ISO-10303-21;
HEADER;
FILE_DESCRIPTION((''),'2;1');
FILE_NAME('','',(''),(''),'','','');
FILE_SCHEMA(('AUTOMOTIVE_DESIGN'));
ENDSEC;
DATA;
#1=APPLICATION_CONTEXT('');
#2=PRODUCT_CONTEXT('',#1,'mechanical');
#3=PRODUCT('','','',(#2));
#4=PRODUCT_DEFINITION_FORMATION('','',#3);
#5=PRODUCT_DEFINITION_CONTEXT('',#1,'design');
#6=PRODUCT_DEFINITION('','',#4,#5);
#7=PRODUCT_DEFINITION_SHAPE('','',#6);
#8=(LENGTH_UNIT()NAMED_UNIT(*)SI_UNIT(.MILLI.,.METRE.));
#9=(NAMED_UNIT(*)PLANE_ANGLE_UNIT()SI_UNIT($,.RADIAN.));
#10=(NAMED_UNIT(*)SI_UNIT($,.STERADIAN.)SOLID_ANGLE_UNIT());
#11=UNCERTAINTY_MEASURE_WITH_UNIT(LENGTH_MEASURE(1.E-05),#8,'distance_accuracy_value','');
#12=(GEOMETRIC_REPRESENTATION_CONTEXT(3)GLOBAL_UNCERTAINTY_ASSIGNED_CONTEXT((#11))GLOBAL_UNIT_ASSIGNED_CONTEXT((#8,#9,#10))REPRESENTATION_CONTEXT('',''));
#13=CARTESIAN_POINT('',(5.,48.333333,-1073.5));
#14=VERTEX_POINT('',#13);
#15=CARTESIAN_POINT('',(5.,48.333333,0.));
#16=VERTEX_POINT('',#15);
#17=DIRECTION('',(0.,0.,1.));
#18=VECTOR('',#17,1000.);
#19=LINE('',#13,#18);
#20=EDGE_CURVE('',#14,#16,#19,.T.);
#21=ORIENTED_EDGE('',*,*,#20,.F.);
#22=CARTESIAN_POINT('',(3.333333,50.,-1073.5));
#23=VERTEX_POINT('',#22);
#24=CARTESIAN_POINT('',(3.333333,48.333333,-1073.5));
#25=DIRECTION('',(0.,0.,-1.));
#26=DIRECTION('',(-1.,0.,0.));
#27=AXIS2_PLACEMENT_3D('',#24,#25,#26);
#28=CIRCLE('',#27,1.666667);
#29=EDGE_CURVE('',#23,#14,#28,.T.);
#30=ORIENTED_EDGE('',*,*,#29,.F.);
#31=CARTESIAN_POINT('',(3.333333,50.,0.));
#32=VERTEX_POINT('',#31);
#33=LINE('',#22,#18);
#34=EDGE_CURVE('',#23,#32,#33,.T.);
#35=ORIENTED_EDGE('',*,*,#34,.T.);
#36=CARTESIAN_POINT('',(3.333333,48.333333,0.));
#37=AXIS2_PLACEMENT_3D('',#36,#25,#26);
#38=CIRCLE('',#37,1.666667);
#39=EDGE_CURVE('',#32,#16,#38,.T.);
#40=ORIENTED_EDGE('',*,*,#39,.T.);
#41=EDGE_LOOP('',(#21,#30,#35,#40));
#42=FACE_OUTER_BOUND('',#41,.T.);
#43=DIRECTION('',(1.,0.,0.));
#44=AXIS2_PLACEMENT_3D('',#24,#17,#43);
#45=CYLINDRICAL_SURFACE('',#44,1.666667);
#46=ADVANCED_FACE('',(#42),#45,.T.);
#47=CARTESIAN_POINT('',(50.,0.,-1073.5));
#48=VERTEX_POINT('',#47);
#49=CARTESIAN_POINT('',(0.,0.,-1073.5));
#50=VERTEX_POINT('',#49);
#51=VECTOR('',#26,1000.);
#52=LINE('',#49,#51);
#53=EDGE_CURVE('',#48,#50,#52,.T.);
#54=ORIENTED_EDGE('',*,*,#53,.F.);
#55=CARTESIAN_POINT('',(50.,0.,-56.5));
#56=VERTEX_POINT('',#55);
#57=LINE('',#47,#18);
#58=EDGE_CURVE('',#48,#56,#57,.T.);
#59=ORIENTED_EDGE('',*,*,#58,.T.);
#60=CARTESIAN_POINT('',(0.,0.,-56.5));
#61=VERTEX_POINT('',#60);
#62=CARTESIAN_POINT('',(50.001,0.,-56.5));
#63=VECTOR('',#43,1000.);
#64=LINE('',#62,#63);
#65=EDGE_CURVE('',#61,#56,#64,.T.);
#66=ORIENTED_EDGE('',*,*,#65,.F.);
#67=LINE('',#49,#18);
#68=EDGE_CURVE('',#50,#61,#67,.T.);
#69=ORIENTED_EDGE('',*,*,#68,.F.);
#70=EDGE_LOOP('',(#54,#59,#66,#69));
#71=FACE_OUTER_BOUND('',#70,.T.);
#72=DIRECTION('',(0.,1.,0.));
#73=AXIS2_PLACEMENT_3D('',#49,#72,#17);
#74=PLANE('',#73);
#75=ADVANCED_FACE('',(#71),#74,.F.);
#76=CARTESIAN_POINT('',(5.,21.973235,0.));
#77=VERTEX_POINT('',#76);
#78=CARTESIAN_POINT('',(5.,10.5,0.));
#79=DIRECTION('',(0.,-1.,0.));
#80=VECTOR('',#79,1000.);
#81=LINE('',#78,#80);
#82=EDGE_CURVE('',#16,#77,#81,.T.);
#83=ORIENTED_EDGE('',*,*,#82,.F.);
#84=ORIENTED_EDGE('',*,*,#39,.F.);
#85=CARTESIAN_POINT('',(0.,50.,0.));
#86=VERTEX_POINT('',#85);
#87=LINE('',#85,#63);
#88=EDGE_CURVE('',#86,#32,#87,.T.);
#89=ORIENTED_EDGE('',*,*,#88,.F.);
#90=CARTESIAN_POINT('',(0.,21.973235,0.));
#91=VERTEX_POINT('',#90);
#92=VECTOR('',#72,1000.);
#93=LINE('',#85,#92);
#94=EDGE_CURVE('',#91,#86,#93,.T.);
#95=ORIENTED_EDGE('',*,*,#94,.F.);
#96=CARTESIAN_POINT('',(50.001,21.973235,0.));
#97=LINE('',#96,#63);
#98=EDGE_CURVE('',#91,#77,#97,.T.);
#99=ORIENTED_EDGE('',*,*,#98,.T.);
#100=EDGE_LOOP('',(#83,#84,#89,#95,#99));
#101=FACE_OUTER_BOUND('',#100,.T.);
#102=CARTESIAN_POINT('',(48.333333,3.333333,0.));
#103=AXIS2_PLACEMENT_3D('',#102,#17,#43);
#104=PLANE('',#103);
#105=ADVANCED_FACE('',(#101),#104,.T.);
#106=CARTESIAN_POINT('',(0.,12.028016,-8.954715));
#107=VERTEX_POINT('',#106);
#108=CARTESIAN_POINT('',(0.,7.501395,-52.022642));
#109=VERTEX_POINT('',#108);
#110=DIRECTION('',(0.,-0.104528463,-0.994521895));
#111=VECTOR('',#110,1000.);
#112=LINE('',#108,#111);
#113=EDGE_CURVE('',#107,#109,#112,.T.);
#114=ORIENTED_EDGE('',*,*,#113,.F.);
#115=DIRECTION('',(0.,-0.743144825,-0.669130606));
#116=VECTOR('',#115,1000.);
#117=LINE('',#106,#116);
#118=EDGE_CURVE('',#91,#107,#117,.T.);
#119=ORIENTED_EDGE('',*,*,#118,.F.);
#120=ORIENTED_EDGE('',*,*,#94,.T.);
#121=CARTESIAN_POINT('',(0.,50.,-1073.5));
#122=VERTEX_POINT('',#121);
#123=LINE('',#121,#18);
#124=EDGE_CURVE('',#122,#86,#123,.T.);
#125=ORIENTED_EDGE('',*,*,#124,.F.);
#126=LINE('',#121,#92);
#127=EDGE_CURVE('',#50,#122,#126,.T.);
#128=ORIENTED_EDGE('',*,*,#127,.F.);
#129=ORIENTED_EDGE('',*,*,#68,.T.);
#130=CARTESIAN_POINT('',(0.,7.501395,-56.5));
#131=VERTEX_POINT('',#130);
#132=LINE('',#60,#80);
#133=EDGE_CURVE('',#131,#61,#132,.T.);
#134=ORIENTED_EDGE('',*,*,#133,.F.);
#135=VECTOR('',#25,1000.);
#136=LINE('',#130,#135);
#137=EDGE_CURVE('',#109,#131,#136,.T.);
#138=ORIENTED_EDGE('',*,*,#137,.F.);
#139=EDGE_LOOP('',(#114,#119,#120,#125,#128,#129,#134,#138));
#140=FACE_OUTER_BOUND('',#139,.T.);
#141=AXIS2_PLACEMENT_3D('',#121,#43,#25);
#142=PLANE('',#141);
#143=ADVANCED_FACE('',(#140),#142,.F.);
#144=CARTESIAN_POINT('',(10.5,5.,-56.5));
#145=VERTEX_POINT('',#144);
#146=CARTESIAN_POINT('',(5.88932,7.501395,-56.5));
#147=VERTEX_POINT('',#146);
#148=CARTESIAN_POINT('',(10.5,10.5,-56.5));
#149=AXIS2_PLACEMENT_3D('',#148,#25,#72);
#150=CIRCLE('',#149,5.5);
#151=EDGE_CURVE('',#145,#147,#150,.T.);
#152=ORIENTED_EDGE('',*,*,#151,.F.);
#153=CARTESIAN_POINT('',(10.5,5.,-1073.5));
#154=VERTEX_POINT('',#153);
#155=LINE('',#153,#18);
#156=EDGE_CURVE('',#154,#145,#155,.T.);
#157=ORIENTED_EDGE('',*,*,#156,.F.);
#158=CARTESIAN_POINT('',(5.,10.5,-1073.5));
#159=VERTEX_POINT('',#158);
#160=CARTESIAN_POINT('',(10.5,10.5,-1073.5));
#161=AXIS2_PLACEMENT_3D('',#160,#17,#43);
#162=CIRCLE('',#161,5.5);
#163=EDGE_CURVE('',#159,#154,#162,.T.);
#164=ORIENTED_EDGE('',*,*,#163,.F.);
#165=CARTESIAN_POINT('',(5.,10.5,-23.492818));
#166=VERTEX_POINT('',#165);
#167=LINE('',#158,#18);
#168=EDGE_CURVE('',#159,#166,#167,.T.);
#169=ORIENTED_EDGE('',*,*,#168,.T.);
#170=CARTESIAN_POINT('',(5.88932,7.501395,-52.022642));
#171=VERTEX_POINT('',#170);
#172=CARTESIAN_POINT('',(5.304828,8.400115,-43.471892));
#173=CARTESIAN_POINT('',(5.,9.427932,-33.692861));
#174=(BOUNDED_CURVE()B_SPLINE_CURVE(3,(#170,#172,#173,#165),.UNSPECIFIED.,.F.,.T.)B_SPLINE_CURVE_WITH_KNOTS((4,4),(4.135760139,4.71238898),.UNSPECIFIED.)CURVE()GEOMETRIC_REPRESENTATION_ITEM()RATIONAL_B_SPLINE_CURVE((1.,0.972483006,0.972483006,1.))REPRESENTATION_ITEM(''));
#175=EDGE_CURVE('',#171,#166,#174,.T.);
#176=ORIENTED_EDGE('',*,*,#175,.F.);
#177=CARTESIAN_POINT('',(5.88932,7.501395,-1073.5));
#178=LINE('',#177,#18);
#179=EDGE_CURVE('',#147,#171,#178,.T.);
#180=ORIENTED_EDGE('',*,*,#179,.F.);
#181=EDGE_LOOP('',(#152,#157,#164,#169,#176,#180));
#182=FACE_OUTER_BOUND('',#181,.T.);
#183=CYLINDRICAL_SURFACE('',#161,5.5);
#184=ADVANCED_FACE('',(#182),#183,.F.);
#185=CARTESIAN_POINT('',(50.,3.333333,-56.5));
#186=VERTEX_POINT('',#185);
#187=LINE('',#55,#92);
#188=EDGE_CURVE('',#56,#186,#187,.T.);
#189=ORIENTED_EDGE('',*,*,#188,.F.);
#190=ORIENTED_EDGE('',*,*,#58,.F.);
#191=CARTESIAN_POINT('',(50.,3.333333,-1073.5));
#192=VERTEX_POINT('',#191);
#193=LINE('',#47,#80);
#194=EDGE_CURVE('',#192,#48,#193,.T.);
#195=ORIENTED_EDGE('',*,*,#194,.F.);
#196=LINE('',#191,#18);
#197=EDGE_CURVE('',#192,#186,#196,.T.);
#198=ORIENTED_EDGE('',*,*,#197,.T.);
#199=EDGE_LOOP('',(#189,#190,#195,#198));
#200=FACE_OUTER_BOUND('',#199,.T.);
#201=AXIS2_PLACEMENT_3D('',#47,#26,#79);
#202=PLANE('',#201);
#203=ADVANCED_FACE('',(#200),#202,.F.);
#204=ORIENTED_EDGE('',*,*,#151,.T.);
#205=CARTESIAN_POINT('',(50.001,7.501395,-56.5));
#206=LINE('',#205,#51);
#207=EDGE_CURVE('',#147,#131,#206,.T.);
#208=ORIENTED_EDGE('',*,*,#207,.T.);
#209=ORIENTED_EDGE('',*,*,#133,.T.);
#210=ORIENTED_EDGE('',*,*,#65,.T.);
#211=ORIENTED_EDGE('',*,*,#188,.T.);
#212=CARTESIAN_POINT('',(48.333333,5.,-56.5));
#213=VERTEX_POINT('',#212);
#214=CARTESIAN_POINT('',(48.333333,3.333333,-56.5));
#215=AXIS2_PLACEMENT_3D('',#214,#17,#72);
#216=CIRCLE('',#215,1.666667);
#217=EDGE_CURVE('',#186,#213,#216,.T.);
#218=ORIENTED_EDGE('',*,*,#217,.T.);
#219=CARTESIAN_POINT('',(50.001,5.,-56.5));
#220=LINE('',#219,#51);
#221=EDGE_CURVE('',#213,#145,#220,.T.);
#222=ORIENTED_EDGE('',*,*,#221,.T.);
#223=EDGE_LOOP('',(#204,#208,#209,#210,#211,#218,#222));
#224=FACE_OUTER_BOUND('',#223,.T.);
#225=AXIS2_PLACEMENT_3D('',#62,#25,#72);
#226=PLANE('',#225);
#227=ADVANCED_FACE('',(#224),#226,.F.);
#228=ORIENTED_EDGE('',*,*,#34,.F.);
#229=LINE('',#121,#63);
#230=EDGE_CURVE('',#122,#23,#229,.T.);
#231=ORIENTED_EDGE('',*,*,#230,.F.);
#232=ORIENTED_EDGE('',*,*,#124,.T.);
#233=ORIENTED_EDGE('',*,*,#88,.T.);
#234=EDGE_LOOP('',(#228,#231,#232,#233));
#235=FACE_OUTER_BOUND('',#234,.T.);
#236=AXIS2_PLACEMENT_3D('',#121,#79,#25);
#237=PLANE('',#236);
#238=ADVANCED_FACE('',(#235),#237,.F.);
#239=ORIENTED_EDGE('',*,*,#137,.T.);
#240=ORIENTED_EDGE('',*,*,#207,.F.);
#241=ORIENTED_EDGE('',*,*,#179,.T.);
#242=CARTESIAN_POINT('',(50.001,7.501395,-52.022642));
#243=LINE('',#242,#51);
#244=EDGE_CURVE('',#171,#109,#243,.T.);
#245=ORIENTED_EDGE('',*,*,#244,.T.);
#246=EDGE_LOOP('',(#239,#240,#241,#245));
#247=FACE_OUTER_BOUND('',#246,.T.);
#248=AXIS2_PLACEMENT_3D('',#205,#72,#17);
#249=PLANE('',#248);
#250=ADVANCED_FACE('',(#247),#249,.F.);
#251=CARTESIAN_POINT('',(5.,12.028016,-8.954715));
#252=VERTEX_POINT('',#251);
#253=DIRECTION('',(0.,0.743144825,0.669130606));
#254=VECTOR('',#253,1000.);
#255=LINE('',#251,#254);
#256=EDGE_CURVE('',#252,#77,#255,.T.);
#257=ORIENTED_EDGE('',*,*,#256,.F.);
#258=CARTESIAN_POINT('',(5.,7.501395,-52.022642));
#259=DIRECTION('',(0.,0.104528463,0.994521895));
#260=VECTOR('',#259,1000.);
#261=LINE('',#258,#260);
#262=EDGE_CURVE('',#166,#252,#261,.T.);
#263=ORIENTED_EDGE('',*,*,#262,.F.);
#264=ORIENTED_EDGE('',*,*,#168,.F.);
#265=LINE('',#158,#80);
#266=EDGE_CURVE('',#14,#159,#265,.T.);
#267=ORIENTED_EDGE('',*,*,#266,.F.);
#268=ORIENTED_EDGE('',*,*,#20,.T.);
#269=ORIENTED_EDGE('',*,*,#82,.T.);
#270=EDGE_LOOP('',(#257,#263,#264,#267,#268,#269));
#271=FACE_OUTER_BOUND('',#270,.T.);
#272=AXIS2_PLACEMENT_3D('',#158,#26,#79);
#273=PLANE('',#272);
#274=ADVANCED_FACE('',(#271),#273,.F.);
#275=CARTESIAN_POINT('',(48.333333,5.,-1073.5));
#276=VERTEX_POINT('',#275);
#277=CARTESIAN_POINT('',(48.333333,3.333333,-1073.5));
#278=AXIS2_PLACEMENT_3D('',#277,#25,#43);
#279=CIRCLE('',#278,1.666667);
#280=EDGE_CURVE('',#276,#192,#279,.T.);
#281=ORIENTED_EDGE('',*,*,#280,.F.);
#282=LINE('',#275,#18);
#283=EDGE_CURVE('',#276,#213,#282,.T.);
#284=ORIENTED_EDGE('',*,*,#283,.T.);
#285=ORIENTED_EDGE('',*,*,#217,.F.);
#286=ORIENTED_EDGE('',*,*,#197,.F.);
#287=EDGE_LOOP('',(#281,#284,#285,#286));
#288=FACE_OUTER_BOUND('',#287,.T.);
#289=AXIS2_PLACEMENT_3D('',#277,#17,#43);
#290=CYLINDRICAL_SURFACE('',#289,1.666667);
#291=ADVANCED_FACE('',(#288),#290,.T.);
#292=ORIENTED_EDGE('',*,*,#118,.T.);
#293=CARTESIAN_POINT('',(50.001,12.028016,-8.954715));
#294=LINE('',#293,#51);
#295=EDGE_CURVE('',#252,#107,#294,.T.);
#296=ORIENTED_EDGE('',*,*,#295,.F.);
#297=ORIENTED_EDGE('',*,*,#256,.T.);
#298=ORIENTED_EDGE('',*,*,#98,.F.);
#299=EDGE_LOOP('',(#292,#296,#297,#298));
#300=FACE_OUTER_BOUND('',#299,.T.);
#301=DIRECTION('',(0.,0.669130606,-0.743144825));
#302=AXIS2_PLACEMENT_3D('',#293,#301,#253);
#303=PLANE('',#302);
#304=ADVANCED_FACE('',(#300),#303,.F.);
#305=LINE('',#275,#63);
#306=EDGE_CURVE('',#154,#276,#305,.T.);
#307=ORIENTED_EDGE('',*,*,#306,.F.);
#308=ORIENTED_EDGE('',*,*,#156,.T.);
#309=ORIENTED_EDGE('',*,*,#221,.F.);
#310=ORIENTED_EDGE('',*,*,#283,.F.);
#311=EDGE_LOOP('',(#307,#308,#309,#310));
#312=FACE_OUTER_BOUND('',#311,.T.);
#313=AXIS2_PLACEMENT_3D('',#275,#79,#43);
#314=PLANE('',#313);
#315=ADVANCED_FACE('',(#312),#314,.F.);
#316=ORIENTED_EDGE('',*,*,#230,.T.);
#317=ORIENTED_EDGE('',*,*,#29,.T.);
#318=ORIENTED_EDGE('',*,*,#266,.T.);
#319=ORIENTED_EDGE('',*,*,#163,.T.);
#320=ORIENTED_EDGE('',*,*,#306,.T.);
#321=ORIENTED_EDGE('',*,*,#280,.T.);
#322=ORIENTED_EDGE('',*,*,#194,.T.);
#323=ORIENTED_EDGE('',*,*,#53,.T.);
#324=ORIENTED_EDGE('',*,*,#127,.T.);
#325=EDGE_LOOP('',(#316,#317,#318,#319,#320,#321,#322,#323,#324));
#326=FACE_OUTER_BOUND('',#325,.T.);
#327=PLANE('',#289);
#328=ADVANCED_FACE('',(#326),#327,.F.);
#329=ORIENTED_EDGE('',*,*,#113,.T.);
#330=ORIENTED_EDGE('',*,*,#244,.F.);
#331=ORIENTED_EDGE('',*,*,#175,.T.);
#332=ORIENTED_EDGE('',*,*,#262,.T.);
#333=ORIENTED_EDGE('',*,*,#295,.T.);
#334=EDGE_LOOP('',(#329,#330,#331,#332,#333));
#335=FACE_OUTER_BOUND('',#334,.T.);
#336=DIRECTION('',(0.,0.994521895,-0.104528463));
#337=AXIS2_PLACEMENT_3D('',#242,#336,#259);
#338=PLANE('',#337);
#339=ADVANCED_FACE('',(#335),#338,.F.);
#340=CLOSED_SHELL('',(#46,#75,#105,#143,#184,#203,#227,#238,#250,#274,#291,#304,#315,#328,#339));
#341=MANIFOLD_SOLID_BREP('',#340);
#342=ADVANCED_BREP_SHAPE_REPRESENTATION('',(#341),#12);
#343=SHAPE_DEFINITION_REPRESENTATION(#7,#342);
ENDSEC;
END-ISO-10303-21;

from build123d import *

# Parameters (mm, degrees)
GBT706_2008_050_5_1_DEPTH = 1073.5
CUT_EXTRUDE_1_REACH       = 1077.826


with BuildPart() as part:
    # Sketch1 → Gbt706-2008 热轧等边角钢 050×5(1) (new body)
    with BuildSketch(Plane.YX):
        with BuildLine():
            Line((0, 0), (0, 50))
            Line((0, 50), (3.333333333, 50))
            ThreePointArc((3.333333333, 50), (4.511844635, 49.511844635), (5, 48.333333333))
            Line((5, 48.333333333), (5, 10.5))
            ThreePointArc((5, 10.5), (6.610912703, 6.610912703), (10.5, 5))
            Line((10.5, 5), (48.333333333, 5))
            ThreePointArc((48.333333333, 5), (49.511844635, 4.511844635), (50, 3.333333333))
            Line((50, 3.333333333), (50, 0))
            Line((50, 0), (0, 0))
        make_face()
    extrude(amount=GBT706_2008_050_5_1_DEPTH)

    # 草图3 → 切除-拉伸1 (cut, up to next)
    with BuildSketch(Plane.ZY, mode=Mode.PRIVATE) as cut_extrude_1_sk1:
        Polygon((-56.5, 0), (-56.5, 7.501394609), (-52.022642316, 7.501394609), (-8.954715367, 12.028016136), (0, 21.973235089), (20, 21.973235089), (20, -8.026764911), (-56.5, -8.026764911), align=None)
    cut_extrude_1_tool1 = extrude(cut_extrude_1_sk1.sketch, amount=-CUT_EXTRUDE_1_REACH, mode=Mode.PRIVATE) & part.part
    add(cut_extrude_1_tool1.solids().sort_by_distance((0, 3.560964, -12.87534))[0], mode=Mode.SUBTRACT)


solid = part.part
